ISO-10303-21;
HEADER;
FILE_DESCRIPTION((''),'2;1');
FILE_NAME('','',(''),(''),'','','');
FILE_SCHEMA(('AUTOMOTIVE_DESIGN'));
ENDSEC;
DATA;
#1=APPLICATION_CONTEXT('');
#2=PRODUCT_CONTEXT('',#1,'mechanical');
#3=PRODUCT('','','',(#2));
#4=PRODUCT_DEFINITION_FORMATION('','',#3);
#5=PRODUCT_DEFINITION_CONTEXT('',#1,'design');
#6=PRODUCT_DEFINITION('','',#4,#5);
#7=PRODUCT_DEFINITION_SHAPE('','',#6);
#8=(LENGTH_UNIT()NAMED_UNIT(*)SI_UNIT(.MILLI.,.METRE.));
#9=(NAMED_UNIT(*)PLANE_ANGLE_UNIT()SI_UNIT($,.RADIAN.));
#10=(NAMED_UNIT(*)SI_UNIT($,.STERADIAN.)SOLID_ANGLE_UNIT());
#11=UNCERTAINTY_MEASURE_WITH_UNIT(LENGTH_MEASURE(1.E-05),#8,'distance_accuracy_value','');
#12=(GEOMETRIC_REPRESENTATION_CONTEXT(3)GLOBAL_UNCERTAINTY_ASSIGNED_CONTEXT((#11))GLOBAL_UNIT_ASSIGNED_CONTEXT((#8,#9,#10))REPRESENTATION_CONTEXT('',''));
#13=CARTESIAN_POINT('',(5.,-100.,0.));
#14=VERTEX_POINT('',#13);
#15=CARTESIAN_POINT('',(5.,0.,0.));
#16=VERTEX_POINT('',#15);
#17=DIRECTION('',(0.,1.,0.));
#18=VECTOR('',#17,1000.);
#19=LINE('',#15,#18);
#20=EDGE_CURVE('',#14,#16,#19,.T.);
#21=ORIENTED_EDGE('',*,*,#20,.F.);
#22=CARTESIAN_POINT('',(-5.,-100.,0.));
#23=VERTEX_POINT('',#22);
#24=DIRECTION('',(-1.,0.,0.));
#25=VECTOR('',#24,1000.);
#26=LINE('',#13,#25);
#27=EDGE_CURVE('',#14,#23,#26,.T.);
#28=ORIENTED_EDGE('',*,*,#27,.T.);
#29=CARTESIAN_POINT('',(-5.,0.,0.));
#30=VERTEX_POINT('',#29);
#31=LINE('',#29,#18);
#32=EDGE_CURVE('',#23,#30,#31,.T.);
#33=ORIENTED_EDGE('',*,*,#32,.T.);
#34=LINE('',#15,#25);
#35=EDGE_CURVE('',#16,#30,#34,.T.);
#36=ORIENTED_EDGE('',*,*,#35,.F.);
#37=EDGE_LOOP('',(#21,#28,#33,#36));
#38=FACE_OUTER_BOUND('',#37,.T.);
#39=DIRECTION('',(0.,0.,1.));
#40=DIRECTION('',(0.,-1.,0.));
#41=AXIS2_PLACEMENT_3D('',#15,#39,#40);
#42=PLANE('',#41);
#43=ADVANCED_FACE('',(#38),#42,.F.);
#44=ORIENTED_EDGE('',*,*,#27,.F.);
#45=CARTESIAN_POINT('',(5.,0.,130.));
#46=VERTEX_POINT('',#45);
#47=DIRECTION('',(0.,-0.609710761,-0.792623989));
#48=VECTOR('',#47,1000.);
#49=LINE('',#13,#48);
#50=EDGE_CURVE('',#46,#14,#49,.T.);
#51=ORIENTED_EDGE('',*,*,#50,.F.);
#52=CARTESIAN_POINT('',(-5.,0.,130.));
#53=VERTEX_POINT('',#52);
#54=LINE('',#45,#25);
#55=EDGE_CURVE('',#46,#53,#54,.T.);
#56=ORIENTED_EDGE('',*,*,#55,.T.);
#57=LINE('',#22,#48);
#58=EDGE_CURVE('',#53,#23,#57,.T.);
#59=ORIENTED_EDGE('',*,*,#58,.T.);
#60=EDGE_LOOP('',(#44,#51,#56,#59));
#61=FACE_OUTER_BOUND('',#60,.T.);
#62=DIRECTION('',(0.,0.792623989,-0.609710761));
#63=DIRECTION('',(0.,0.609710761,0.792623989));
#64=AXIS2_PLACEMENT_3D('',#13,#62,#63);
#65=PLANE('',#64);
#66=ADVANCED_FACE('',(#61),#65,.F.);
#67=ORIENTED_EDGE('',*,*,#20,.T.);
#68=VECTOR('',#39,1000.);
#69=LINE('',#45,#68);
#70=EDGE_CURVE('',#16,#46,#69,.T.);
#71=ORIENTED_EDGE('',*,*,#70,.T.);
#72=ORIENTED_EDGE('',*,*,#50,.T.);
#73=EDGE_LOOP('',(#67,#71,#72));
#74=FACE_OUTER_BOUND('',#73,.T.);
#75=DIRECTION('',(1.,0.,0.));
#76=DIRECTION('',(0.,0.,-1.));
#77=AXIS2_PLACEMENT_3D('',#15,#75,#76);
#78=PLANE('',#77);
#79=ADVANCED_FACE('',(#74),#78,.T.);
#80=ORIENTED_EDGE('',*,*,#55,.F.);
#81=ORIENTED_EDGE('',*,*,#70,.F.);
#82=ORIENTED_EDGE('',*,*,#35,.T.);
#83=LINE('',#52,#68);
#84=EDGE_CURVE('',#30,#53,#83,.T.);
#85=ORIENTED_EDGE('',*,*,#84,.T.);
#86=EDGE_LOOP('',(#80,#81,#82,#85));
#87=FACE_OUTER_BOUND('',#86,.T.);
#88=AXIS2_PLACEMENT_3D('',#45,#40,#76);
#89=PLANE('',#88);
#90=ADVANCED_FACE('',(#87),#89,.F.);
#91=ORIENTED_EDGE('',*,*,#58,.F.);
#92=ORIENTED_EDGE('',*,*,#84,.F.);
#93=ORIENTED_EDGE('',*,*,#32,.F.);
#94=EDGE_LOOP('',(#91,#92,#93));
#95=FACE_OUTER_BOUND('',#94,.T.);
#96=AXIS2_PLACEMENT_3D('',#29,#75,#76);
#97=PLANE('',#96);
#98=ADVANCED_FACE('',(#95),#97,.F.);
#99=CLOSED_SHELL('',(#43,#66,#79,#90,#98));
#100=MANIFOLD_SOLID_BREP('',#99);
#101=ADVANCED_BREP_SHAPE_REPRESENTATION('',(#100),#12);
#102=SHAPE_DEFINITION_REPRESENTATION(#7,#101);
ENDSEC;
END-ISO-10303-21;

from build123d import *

# Parameters (mm, degrees)
BOSS_EXTRUDE1_DEPTH = 5


with BuildPart() as part:
    # Sketch1 → Boss-Extrude1 (new, symmetric)
    with BuildSketch(Plane(origin=(0, 0, 0), x_dir=(0, 0, -1), z_dir=(1, 0, 0))):
        Polygon((-130, 0), (0, 0), (0, -100), align=None)
    extrude(amount=BOSS_EXTRUDE1_DEPTH, both=True)


solid = part.part
